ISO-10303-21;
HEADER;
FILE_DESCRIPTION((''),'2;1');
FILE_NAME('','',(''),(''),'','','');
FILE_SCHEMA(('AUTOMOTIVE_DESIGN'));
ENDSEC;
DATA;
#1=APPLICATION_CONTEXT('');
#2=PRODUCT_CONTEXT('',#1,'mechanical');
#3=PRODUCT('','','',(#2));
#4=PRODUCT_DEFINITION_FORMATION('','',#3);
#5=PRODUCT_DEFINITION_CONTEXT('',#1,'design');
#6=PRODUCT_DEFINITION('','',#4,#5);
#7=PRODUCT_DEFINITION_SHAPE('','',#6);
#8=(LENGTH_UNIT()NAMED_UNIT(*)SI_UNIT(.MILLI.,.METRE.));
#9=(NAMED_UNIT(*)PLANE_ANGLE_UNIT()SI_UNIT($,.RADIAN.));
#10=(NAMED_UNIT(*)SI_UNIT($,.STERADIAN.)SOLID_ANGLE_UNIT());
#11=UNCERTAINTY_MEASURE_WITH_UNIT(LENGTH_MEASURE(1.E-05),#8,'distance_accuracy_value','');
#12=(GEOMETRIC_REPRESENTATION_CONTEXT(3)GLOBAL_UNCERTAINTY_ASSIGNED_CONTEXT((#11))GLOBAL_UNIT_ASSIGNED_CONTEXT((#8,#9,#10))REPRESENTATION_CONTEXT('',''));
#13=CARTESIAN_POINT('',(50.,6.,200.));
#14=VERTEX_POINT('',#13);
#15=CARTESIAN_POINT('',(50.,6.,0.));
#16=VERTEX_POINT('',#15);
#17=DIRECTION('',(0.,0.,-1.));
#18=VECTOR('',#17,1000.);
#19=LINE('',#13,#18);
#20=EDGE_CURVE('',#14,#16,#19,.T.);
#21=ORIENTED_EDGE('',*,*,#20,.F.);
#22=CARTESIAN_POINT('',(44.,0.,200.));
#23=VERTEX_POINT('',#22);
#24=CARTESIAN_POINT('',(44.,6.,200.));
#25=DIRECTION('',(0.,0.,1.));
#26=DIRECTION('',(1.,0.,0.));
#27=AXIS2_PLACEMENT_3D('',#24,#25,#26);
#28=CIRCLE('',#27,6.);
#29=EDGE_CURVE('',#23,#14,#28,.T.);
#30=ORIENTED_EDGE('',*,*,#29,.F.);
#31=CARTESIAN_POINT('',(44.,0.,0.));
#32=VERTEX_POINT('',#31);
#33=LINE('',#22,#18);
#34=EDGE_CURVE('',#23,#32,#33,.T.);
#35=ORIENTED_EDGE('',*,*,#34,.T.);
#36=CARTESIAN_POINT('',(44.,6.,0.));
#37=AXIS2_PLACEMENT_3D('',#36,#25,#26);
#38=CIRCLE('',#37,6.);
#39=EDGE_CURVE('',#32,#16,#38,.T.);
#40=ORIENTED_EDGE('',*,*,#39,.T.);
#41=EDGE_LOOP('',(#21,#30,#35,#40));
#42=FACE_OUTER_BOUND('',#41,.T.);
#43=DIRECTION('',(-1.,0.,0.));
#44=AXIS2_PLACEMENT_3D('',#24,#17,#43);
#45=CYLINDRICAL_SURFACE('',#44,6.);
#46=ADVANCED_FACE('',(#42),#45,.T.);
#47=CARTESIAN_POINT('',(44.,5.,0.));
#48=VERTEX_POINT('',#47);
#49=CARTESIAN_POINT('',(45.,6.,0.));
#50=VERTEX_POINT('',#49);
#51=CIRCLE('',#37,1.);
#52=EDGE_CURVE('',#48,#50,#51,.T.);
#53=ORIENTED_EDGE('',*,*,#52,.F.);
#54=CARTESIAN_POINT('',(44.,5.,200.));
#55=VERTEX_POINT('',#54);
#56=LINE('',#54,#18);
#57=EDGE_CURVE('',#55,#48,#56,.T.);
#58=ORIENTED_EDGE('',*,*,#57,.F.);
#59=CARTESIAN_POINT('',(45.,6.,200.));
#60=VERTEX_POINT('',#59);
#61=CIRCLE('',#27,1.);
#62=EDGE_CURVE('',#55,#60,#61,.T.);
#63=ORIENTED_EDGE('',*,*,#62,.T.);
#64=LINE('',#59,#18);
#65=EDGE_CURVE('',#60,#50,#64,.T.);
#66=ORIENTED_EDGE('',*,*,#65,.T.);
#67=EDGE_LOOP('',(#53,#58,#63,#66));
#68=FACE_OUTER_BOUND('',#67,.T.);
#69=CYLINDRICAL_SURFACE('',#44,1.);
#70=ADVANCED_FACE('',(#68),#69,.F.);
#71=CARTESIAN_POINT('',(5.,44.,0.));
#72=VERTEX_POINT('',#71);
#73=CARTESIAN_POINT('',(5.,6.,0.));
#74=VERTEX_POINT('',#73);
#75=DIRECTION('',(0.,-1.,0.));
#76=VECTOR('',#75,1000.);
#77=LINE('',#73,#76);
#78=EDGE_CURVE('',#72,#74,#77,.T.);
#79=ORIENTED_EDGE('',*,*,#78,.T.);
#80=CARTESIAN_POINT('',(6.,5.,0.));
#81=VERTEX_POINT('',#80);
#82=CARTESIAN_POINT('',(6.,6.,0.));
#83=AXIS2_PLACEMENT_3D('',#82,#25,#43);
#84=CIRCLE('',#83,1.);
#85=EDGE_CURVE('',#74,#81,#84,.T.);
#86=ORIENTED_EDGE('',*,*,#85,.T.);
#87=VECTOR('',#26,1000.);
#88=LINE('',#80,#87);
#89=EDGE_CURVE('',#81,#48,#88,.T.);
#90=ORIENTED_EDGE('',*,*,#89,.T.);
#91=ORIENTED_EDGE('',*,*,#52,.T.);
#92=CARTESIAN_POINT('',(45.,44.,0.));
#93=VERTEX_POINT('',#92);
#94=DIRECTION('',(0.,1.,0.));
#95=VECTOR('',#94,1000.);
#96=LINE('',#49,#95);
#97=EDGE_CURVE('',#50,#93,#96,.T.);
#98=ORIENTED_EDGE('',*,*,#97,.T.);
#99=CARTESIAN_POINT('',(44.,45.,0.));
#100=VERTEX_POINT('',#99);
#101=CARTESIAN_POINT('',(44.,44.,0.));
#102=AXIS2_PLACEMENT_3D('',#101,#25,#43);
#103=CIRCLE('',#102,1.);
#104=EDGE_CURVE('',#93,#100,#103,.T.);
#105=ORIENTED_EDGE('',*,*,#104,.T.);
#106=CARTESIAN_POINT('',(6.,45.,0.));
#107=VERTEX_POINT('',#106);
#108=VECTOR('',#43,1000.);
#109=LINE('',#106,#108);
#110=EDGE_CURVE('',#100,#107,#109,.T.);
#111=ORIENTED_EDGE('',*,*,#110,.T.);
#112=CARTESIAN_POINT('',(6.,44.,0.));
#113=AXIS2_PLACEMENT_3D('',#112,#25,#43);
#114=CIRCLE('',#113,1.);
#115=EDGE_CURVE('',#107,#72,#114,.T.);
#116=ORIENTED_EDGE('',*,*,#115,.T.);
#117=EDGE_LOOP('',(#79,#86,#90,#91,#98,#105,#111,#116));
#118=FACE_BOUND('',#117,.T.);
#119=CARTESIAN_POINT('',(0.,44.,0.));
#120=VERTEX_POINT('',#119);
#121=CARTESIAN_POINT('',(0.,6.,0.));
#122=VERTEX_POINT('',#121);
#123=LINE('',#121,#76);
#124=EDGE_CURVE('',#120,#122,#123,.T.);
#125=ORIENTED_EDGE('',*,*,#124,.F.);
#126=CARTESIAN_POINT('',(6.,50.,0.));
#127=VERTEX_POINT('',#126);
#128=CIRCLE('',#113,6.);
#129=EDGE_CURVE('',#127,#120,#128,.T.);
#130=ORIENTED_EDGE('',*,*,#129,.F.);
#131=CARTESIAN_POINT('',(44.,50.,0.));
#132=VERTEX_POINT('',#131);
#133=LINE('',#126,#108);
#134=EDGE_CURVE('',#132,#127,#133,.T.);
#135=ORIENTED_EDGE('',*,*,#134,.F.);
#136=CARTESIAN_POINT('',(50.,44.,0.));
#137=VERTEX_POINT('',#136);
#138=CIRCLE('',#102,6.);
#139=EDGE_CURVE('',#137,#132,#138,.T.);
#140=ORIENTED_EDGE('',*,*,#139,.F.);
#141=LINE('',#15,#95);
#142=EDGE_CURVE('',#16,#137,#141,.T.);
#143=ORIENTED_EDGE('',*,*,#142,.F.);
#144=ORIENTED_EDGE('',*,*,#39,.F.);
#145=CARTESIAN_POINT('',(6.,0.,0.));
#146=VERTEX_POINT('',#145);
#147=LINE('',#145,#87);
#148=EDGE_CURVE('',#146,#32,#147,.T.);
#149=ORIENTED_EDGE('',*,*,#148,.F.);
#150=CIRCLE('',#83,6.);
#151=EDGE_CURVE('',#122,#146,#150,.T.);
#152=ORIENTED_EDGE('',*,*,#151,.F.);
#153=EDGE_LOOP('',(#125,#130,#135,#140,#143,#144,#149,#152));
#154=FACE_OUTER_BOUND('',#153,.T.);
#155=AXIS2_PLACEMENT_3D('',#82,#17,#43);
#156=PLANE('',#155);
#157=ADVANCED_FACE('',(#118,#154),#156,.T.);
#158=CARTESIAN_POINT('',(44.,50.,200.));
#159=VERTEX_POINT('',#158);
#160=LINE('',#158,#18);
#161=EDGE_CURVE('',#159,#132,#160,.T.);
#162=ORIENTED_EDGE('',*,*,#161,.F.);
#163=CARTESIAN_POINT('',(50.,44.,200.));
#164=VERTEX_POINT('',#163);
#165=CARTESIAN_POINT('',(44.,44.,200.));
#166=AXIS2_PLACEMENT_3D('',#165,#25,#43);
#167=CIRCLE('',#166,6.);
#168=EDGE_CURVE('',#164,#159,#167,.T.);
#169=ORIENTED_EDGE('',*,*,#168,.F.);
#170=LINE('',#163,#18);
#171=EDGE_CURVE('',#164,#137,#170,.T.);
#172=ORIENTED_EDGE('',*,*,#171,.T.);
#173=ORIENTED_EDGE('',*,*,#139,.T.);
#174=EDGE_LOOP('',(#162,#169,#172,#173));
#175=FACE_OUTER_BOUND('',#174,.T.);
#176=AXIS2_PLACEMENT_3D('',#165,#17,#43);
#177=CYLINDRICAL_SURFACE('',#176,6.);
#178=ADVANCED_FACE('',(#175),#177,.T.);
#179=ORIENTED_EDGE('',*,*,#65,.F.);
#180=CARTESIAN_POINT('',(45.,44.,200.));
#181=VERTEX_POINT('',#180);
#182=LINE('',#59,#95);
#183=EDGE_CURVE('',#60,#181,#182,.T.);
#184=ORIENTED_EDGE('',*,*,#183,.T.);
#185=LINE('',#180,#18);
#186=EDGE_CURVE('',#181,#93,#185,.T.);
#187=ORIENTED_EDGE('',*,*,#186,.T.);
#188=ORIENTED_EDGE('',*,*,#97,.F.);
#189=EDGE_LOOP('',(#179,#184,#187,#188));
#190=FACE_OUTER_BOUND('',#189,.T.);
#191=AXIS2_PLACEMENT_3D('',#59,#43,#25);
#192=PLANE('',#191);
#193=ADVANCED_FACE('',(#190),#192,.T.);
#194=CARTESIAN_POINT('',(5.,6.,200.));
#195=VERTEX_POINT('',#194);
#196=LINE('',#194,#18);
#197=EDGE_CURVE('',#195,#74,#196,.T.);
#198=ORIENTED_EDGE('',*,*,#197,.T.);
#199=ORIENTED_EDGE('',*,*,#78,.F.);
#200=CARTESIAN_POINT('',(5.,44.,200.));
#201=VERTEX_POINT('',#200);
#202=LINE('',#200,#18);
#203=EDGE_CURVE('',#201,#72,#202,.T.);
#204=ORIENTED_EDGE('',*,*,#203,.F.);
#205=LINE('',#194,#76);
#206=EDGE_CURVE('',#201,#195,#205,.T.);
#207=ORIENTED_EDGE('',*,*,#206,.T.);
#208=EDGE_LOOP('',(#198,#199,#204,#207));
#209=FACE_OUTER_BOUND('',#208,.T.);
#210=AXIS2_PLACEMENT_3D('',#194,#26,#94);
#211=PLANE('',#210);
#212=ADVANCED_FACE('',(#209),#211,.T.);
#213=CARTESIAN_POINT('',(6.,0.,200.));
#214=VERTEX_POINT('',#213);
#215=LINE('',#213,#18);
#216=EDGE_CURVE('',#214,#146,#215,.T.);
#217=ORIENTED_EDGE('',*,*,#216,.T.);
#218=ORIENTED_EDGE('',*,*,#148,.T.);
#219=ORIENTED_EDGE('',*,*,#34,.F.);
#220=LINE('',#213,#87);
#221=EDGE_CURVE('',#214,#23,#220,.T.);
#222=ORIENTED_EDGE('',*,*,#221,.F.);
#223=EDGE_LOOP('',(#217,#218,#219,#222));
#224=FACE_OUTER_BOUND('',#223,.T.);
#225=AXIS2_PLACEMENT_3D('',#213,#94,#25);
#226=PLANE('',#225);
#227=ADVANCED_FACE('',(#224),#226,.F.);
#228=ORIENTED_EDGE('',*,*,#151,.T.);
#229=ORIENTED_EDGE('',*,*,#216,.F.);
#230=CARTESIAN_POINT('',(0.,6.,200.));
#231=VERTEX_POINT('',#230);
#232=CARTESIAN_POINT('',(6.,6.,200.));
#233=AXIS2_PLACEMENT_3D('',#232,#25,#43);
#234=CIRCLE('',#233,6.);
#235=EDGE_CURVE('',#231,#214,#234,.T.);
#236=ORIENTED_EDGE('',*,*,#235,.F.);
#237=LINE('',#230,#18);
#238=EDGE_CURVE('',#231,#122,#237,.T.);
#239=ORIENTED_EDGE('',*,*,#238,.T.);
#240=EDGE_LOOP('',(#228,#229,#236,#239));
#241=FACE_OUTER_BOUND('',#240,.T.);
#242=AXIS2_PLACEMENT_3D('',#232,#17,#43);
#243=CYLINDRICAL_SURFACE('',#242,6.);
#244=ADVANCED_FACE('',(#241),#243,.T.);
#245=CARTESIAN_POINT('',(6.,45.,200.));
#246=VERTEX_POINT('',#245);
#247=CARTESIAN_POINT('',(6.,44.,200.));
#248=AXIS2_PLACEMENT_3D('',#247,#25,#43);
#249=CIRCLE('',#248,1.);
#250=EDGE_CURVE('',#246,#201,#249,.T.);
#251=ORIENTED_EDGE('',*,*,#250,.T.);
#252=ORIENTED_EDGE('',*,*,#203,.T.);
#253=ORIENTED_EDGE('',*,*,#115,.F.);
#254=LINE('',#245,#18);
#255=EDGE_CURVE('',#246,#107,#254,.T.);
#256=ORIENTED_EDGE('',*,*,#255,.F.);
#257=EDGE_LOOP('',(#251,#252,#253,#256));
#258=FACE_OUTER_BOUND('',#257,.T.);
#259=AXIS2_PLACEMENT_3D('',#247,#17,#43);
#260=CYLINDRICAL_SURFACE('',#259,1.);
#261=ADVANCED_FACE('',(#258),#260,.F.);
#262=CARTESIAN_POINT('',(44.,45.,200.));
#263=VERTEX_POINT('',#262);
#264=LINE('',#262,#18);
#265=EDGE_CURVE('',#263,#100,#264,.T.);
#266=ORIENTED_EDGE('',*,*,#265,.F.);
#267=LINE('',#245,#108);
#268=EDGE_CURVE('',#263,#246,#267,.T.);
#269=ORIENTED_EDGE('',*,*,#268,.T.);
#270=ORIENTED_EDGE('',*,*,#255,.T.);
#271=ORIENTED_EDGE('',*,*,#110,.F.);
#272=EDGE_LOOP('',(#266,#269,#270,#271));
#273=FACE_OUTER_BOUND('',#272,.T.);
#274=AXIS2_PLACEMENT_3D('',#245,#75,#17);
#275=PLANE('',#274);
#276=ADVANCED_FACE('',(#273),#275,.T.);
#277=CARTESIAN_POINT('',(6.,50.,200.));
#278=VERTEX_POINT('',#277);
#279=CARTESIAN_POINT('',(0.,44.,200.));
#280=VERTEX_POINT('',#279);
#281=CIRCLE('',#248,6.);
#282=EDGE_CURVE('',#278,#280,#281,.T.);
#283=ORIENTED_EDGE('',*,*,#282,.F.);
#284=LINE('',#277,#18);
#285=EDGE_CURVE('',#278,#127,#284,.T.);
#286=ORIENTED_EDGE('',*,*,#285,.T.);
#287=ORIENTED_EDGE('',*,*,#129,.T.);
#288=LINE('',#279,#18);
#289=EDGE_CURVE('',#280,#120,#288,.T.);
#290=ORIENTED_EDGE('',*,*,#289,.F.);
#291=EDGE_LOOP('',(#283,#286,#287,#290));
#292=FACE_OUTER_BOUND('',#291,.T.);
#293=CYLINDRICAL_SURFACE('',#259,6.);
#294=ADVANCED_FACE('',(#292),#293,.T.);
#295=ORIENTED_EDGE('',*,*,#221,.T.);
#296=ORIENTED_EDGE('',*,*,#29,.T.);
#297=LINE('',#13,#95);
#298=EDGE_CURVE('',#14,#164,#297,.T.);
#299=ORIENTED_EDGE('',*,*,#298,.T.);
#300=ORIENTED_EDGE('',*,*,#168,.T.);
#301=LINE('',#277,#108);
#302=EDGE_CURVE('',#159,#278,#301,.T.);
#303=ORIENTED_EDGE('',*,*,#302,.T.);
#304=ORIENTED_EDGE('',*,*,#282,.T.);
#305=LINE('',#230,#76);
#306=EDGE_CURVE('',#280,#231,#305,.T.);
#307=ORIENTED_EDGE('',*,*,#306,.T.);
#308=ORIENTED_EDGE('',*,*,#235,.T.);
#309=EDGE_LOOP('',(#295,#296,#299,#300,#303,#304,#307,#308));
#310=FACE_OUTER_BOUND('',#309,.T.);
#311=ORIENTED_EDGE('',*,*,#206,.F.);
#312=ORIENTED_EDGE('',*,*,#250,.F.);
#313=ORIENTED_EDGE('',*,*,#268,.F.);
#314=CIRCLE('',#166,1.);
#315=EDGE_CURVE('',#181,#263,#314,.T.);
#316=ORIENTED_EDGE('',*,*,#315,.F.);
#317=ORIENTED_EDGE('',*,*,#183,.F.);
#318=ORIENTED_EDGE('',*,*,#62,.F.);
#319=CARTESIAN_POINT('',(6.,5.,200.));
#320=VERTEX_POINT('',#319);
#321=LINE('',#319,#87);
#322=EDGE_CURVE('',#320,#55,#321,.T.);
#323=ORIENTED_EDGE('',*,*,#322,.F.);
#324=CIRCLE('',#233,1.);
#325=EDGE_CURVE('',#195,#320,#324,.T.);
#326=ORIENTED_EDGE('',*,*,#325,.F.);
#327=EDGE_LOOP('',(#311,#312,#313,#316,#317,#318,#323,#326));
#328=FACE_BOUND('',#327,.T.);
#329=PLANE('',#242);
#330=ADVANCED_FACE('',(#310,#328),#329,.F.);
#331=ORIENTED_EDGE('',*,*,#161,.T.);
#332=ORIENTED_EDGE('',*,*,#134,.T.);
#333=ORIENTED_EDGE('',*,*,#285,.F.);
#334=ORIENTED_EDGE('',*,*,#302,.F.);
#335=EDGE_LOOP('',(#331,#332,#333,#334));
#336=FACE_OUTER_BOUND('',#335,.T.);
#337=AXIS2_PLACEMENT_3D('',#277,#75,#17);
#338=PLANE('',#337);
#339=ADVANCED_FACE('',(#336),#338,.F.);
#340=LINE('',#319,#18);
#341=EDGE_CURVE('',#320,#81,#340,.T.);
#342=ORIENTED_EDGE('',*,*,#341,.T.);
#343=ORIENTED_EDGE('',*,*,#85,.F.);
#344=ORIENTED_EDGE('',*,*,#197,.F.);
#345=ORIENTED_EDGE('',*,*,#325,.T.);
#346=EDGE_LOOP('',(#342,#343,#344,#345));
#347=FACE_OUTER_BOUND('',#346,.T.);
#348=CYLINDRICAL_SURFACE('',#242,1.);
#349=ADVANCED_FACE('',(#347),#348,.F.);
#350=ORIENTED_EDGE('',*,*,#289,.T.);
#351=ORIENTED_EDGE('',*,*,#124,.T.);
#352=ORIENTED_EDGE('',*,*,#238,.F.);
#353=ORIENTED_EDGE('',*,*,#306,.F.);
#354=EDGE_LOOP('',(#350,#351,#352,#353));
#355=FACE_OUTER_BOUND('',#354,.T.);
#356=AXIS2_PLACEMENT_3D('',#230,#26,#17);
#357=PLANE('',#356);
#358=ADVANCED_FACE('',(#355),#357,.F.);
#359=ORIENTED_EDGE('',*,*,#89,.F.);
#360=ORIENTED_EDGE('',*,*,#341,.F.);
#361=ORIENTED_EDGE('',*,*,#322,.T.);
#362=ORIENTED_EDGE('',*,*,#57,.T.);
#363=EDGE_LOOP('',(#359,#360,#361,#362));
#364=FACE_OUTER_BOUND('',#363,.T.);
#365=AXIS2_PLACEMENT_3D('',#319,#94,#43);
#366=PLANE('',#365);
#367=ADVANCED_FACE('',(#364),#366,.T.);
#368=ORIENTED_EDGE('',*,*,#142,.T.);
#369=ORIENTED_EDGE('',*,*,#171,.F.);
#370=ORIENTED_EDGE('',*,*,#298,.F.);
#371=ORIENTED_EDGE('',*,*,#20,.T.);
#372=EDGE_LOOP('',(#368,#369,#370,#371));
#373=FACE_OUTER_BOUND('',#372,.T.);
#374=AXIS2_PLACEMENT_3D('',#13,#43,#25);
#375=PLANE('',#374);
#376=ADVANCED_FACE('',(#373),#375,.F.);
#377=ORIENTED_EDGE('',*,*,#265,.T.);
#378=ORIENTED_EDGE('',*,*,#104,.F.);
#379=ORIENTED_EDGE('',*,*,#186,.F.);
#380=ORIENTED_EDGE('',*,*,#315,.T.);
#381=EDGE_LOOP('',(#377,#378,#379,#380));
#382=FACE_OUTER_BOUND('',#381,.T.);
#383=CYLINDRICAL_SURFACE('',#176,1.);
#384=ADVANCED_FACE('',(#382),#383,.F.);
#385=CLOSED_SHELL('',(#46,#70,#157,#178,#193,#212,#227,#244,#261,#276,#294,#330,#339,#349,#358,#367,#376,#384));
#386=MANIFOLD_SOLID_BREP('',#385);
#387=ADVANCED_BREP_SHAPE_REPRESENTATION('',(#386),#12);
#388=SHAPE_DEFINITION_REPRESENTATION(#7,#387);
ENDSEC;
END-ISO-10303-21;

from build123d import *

# Parameters (mm, degrees)
BOSS_EXTRUDE1_DEPTH = 200


with BuildPart() as part:
    # Sketch1 → Boss-Extrude1 (new body)
    with BuildSketch(Plane.XY):
        with BuildLine():
            Line((6, 0), (44, 0))
            ThreePointArc((44, 0), (48.242640687, 1.757359313), (50, 6))
            Line((50, 6), (50, 44))
            ThreePointArc((50, 44), (48.242640687, 48.242640687), (44, 50))
            Line((44, 50), (6, 50))
            ThreePointArc((6, 50), (1.757359313, 48.242640687), (0, 44))
            Line((0, 44), (0, 6))
            ThreePointArc((0, 6), (1.757359313, 1.757359313), (6, 0))
        make_face()
        with BuildLine():
            Line((6, 45), (44, 45))
            ThreePointArc((44, 45), (44.707106781, 44.707106781), (45, 44))
            Line((45, 44), (45, 6))
            ThreePointArc((45, 6), (44.707106781, 5.292893219), (44, 5))
            Line((44, 5), (6, 5))
            ThreePointArc((6, 5), (5.292893219, 5.292893219), (5, 6))
            Line((5, 6), (5, 44))
            ThreePointArc((5, 44), (5.292893219, 44.707106781), (6, 45))
        make_face(mode=Mode.SUBTRACT)
    extrude(amount=BOSS_EXTRUDE1_DEPTH)


solid = part.part
